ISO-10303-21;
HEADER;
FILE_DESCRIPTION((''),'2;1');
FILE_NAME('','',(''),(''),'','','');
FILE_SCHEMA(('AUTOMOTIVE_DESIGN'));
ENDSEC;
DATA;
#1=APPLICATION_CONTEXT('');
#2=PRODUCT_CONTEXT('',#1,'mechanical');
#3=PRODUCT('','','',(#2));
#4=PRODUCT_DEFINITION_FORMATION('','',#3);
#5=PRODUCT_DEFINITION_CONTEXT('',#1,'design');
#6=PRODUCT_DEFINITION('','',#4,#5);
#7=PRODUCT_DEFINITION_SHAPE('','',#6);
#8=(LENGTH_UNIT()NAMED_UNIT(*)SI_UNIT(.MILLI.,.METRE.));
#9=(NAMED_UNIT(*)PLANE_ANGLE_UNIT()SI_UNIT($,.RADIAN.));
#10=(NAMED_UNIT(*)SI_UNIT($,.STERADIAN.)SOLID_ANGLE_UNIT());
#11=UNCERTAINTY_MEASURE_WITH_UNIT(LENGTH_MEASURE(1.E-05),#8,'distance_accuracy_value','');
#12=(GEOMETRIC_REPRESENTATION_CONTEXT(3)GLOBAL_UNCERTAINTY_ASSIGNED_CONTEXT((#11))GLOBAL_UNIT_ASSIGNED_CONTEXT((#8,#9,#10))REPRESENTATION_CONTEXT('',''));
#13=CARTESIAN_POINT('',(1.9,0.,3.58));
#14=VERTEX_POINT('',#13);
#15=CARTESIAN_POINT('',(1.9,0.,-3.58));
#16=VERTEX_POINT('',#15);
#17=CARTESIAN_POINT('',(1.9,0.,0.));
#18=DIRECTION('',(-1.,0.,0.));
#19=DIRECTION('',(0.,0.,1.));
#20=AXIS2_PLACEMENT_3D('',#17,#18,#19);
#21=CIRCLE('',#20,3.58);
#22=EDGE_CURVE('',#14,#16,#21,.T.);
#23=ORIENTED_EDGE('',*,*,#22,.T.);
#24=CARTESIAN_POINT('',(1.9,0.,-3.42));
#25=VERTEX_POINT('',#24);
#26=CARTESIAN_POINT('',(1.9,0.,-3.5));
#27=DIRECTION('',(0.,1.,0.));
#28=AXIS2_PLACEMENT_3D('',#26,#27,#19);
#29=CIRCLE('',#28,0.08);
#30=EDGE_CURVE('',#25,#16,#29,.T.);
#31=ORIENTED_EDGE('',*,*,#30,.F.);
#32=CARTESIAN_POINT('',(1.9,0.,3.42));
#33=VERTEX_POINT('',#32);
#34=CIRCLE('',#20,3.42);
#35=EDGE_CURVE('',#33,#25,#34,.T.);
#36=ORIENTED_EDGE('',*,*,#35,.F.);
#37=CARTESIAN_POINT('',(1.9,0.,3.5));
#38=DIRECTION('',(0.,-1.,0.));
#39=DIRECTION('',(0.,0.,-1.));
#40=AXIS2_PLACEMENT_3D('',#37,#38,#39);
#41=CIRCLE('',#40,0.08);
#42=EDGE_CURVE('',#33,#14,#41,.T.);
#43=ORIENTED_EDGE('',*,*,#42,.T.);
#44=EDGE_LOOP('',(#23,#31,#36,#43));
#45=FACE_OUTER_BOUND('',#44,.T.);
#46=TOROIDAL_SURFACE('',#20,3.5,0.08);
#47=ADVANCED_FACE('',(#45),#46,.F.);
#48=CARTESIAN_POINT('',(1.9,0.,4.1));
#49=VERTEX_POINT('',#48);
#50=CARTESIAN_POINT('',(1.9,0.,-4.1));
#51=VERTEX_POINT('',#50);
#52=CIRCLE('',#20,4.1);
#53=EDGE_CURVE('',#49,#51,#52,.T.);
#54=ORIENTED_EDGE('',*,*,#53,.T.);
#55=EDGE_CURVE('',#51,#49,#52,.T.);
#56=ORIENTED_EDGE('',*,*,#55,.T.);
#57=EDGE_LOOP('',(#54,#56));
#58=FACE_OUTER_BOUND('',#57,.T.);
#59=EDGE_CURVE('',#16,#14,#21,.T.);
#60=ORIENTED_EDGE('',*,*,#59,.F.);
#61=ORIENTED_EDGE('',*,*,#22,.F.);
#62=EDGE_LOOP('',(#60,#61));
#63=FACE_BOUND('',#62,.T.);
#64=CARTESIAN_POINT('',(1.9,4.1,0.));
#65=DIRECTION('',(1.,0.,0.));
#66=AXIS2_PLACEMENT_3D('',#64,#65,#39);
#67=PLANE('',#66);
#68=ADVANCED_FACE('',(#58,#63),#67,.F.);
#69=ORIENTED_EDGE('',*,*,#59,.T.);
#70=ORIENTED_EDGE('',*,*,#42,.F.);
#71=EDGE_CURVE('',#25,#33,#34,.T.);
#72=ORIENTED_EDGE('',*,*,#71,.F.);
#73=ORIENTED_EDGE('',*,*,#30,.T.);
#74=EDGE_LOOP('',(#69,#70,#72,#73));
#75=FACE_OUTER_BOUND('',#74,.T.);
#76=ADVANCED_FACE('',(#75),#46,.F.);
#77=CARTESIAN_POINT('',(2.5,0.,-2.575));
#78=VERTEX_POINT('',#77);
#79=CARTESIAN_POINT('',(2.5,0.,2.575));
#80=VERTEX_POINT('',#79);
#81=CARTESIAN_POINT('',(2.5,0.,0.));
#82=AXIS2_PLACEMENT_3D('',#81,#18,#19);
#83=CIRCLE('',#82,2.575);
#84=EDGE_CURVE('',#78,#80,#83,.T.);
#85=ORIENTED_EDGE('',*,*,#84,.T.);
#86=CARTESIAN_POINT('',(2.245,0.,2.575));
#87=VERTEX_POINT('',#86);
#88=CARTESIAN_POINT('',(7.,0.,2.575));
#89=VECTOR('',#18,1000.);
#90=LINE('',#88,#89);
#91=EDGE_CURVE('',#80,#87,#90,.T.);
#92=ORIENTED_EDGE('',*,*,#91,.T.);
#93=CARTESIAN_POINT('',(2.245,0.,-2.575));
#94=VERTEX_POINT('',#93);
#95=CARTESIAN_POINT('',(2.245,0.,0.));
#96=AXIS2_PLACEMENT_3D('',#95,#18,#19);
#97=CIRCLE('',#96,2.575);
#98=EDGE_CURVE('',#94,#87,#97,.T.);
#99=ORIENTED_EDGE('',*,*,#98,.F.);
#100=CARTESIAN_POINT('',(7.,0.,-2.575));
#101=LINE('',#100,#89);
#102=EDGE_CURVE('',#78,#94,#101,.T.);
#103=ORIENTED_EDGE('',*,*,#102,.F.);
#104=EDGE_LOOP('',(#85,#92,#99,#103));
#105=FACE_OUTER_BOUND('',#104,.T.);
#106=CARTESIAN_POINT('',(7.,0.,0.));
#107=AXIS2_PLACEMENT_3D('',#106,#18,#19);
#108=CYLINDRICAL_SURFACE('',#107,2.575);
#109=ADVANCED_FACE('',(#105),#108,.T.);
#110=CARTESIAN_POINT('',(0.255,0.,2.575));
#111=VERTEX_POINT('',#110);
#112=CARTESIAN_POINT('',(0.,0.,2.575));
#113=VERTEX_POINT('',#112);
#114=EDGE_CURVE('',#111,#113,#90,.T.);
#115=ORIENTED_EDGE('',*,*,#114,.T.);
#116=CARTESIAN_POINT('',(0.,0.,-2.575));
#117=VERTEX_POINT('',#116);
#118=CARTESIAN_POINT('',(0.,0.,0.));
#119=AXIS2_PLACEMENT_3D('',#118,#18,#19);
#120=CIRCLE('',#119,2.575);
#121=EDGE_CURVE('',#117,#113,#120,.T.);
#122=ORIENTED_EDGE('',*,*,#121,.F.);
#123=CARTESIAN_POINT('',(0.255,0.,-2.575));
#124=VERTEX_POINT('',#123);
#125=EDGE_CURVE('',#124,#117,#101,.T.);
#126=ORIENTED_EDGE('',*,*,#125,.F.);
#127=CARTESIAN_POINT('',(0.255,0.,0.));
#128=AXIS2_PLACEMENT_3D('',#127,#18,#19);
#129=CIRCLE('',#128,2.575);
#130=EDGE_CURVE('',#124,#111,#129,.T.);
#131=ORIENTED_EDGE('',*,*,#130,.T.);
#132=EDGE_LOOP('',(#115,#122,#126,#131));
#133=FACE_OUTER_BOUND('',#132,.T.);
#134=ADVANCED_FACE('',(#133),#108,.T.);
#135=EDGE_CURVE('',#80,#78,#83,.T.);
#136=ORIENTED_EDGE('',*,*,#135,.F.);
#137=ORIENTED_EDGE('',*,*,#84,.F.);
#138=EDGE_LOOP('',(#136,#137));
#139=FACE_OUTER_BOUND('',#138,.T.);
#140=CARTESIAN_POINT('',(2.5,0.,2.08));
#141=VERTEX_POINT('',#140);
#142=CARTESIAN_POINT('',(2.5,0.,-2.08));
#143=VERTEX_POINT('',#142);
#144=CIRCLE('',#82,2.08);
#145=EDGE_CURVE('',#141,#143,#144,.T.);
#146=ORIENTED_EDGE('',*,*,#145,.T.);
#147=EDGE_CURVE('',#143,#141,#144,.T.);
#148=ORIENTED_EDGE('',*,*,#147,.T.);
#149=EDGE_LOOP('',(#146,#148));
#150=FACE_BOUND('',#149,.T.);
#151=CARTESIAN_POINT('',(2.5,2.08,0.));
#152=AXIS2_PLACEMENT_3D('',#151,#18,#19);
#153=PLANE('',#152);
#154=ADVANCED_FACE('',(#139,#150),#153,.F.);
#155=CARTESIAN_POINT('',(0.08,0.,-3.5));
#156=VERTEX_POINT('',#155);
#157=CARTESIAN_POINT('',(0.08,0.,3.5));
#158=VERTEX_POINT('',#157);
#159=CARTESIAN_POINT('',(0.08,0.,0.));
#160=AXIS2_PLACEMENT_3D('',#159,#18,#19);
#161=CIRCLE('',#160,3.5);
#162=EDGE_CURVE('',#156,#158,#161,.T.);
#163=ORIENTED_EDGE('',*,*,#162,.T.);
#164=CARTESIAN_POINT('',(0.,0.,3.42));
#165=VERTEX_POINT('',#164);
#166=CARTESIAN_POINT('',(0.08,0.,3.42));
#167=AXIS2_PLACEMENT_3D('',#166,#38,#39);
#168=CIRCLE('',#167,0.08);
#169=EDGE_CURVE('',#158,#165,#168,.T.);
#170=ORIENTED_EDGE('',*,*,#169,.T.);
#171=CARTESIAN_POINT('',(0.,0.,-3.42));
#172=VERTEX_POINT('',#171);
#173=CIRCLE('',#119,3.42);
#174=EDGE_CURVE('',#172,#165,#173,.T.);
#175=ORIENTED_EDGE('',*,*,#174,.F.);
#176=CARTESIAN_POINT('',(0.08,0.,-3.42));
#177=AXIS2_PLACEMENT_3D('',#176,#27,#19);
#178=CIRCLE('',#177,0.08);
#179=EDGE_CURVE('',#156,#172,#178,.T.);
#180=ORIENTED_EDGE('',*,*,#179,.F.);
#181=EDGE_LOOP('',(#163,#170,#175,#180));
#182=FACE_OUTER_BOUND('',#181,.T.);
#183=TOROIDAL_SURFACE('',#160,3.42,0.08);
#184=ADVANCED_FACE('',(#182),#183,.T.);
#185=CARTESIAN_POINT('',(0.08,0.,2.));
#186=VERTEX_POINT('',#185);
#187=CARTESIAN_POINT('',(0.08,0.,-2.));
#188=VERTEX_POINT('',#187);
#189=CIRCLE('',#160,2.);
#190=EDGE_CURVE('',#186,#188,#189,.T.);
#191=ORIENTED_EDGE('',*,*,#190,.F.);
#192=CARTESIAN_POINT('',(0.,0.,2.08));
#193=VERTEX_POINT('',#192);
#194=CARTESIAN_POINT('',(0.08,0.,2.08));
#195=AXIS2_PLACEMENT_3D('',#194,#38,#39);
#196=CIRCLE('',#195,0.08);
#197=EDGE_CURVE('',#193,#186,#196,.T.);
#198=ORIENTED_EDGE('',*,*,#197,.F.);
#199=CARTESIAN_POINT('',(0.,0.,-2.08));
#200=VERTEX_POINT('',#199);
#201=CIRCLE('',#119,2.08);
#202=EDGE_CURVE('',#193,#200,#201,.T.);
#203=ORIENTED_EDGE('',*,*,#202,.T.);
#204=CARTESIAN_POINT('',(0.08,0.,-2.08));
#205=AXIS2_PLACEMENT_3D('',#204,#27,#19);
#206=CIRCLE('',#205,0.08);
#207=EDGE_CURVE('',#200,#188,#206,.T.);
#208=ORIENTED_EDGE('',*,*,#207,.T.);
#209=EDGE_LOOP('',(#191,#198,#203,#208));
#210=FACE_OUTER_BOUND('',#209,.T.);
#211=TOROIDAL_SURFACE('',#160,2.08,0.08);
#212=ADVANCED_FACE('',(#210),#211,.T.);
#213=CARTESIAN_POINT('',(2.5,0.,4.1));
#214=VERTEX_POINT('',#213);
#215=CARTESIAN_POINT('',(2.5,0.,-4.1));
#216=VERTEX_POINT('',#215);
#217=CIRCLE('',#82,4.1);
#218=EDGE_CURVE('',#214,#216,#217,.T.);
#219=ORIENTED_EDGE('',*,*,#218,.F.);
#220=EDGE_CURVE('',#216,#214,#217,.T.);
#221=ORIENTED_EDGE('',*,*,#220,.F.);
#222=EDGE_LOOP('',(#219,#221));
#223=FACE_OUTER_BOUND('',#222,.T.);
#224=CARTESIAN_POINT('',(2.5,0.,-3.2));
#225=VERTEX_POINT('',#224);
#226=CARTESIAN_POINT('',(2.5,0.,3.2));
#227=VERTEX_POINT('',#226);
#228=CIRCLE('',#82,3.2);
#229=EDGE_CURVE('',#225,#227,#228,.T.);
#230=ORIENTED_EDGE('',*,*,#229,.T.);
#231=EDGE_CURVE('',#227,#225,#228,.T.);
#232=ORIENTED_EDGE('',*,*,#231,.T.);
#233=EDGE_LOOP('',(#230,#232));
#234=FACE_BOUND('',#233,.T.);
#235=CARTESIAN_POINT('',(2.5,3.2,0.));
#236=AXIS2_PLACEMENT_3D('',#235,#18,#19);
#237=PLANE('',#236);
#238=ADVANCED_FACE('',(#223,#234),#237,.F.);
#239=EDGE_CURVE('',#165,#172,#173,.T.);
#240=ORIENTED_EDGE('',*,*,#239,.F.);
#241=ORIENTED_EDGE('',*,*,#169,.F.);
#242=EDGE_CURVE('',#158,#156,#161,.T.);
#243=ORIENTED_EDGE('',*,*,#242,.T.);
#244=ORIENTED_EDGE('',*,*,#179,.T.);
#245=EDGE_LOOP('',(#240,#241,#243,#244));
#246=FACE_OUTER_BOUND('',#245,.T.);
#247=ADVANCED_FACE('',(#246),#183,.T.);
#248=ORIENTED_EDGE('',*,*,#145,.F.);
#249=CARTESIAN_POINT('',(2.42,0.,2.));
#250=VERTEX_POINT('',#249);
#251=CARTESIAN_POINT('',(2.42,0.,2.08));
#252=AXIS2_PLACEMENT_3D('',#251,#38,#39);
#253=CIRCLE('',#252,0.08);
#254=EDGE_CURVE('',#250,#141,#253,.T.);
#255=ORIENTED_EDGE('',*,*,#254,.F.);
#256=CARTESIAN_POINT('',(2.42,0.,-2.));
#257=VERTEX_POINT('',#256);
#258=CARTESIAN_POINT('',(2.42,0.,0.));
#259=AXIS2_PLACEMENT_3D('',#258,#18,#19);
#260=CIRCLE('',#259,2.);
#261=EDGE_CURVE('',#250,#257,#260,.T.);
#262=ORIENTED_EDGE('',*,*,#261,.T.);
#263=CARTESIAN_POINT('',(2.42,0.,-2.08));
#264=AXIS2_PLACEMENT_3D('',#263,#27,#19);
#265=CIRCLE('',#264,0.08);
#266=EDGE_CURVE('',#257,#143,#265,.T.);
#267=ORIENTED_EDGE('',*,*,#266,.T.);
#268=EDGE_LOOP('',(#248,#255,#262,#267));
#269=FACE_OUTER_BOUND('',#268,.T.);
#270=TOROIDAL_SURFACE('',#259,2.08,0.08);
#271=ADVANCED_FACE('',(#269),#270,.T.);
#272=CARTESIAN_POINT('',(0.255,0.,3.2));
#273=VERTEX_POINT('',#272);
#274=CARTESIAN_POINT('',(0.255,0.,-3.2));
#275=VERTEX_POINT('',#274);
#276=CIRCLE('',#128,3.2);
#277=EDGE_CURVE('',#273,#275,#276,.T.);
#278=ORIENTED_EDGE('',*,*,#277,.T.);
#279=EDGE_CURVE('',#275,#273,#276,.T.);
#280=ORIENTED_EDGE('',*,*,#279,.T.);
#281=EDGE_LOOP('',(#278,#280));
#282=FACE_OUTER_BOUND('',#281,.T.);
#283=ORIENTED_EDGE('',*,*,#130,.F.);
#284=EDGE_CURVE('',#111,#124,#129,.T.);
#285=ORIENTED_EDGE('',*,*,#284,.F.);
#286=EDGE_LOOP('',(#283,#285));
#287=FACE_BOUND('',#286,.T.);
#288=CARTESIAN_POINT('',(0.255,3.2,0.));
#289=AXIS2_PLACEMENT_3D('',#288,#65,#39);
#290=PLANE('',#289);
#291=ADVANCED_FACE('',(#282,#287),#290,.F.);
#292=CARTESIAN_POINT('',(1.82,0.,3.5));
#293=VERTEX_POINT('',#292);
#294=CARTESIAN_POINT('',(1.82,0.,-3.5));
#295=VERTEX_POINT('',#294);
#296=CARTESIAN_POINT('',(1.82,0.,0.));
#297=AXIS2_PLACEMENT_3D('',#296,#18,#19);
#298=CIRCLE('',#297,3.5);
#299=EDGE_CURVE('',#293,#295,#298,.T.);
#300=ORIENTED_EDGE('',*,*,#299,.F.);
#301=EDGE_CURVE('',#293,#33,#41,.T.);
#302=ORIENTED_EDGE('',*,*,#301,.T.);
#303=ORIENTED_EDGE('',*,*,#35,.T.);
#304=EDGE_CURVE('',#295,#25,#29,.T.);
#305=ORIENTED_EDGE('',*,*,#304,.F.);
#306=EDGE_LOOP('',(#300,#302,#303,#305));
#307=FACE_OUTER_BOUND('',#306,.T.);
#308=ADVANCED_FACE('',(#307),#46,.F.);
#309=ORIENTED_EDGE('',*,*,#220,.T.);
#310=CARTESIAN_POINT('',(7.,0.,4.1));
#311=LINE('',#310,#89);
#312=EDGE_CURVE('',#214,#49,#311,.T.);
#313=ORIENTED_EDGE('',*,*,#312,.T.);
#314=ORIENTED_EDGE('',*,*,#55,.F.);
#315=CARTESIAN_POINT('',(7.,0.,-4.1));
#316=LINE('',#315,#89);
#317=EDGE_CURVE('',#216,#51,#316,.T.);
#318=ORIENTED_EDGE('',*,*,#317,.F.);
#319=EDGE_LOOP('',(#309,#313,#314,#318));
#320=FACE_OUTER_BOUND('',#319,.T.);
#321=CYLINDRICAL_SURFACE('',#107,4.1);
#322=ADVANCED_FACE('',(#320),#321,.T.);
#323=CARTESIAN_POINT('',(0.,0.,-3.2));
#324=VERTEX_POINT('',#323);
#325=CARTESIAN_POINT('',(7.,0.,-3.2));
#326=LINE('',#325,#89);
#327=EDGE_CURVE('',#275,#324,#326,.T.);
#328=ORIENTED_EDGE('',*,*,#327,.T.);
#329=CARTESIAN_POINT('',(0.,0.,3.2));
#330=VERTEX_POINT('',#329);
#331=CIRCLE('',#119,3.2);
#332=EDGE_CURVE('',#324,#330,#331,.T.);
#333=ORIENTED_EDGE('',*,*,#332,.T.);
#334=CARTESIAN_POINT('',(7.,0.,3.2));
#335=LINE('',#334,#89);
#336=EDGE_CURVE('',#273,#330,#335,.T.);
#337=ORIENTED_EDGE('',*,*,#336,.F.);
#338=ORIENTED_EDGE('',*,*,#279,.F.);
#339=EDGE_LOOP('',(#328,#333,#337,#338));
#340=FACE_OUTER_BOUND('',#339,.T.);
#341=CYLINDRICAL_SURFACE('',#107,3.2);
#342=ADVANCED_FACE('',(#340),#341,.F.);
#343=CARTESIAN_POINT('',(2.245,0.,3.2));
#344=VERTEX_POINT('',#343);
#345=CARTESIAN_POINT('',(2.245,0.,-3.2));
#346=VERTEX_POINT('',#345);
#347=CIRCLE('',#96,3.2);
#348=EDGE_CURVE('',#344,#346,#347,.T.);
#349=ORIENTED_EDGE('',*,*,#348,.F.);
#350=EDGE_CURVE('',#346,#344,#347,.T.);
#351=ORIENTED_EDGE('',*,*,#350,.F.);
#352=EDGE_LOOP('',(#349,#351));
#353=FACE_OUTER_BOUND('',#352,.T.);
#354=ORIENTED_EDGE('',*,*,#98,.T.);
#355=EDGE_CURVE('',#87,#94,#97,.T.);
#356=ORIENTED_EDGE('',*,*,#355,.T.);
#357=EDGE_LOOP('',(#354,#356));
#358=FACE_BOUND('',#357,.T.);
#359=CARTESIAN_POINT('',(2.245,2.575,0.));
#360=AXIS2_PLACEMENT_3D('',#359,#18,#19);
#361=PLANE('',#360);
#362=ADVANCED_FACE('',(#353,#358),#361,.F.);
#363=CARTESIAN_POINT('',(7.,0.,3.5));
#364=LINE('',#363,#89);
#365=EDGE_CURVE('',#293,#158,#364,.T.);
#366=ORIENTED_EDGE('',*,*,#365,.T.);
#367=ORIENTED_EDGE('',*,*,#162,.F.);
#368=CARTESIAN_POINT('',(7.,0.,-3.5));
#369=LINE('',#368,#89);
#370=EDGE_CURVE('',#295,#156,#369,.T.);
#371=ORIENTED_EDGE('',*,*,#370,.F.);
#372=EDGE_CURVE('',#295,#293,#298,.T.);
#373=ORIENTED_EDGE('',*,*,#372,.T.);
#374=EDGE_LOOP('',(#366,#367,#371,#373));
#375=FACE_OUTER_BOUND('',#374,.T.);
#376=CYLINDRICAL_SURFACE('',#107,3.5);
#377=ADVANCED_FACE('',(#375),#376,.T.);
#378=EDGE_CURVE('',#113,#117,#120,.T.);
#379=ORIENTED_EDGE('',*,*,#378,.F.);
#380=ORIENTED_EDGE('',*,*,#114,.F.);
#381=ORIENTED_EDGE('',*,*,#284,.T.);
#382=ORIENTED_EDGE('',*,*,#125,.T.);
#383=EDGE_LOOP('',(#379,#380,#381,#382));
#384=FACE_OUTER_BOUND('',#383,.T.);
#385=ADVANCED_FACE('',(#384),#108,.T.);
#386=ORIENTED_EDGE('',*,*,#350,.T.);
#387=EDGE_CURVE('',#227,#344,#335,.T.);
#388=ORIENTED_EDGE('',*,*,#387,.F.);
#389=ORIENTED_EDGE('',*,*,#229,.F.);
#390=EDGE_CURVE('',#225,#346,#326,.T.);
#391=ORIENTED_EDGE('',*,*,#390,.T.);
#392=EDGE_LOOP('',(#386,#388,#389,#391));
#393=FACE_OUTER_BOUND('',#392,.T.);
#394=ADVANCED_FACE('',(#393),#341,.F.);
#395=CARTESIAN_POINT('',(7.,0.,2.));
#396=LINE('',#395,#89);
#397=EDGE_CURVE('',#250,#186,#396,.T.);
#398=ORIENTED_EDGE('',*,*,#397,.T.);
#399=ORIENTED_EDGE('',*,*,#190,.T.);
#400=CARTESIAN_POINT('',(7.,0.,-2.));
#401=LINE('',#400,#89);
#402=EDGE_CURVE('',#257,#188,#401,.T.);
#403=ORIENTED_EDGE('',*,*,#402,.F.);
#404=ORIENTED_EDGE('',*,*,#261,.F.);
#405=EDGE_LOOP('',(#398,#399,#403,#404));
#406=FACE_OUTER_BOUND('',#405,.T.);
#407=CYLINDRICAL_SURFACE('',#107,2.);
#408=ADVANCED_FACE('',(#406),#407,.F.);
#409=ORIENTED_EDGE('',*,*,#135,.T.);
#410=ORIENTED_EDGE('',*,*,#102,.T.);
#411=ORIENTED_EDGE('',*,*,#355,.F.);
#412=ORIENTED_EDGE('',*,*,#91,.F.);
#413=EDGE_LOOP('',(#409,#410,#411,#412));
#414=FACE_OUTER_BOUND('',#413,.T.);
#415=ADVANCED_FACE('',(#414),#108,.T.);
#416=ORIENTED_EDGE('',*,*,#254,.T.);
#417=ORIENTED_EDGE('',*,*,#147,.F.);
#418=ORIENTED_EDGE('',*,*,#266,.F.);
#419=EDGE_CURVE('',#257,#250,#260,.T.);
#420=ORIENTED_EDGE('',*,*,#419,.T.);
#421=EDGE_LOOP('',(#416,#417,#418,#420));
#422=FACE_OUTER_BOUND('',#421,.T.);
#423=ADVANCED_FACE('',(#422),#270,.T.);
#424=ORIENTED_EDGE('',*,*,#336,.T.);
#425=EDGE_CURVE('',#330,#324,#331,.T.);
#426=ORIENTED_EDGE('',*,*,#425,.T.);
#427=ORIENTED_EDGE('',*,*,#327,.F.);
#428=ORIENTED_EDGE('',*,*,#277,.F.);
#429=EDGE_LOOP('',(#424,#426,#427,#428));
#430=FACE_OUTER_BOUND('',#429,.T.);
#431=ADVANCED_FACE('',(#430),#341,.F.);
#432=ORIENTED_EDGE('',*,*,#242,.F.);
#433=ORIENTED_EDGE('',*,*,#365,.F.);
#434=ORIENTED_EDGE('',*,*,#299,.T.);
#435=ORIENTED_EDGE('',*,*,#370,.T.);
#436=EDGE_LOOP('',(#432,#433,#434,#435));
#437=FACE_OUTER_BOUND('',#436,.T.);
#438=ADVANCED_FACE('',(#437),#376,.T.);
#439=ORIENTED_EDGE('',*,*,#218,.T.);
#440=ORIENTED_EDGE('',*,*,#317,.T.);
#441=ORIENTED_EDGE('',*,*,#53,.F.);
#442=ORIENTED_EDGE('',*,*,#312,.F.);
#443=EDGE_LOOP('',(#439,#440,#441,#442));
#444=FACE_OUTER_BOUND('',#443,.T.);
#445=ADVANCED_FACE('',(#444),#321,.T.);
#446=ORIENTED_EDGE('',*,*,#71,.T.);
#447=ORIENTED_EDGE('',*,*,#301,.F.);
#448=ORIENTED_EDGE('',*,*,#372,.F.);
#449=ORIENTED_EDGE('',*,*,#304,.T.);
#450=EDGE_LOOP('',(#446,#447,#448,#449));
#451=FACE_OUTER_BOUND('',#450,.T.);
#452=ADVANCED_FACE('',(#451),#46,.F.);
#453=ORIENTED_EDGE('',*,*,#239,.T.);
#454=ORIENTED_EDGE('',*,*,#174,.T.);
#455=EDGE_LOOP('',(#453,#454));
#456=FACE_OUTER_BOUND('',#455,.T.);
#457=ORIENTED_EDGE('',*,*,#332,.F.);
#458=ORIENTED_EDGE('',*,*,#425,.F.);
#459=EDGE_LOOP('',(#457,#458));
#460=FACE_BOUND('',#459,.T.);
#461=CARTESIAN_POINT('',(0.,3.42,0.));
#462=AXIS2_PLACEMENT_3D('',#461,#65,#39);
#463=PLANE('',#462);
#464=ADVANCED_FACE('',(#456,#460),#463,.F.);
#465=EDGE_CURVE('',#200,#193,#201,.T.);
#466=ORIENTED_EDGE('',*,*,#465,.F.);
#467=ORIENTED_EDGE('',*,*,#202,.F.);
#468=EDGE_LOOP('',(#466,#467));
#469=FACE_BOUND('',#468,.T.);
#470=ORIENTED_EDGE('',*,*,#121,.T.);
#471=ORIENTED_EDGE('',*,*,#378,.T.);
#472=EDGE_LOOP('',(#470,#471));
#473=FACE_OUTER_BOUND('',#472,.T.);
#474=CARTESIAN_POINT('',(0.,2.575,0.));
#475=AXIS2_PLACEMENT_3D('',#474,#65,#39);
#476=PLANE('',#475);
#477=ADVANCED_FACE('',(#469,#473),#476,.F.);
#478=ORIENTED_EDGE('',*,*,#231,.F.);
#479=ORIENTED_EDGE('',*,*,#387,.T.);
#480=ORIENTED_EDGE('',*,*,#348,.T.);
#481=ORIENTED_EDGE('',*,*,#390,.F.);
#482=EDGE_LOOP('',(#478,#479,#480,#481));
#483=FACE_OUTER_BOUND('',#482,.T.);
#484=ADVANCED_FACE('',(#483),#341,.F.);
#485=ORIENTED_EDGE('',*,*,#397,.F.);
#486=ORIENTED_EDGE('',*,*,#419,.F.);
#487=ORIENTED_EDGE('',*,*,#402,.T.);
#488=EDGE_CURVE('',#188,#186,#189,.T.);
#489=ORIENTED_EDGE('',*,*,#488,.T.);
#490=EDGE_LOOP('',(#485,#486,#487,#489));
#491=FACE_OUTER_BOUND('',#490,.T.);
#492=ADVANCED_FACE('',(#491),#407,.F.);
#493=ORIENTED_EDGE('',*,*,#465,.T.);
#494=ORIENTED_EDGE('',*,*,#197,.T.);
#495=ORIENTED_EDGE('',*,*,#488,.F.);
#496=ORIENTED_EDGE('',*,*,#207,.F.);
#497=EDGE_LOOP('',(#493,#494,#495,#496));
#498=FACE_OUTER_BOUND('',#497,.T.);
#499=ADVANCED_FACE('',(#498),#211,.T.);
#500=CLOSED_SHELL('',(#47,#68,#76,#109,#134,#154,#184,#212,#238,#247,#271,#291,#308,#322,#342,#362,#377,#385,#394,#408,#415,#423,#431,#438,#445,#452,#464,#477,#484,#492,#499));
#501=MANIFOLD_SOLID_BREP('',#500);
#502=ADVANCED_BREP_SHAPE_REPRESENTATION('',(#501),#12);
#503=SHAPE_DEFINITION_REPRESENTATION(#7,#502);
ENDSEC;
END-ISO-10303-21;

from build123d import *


with BuildPart() as part:
    # Sketch1 → Revolve1 (revolve)
    with BuildSketch(Plane.XY, mode=Mode.PRIVATE) as revolve1_sk:
        with BuildLine():
            Line((0, 3.42), (0, 3.2))
            Line((0, 3.2), (0.255, 3.2))
            Line((0.255, 3.2), (0.255, 2.575))
            Line((0.255, 2.575), (0, 2.575))
            Line((0, 2.575), (0, 2.08))
            ThreePointArc((0, 2.08), (0.023431458, 2.023431458), (0.08, 2))
            Line((0.08, 2), (2.42, 2))
            ThreePointArc((2.42, 2), (2.476568542, 2.023431458), (2.5, 2.08))
            Line((2.5, 2.08), (2.5, 2.575))
            Line((2.5, 2.575), (2.245, 2.575))
            Line((2.245, 2.575), (2.245, 3.2))
            Line((2.245, 3.2), (2.5, 3.2))
            Line((2.5, 3.2), (2.5, 4.1))
            Line((2.5, 4.1), (1.9, 4.1))
            Line((1.9, 4.1), (1.9, 3.58))
            ThreePointArc((1.9, 3.58), (1.956568542, 3.443431458), (1.82, 3.5))
            Line((1.82, 3.5), (0.08, 3.5))
            ThreePointArc((0.08, 3.5), (0.023431458, 3.476568542), (0, 3.42))
        make_face()
    revolve(revolve1_sk.sketch.rotate(Axis((7, 0, 0), (-1, 0, 0)), 270), axis=Axis((7, 0, 0), (-1, 0, 0)))


solid = part.part
